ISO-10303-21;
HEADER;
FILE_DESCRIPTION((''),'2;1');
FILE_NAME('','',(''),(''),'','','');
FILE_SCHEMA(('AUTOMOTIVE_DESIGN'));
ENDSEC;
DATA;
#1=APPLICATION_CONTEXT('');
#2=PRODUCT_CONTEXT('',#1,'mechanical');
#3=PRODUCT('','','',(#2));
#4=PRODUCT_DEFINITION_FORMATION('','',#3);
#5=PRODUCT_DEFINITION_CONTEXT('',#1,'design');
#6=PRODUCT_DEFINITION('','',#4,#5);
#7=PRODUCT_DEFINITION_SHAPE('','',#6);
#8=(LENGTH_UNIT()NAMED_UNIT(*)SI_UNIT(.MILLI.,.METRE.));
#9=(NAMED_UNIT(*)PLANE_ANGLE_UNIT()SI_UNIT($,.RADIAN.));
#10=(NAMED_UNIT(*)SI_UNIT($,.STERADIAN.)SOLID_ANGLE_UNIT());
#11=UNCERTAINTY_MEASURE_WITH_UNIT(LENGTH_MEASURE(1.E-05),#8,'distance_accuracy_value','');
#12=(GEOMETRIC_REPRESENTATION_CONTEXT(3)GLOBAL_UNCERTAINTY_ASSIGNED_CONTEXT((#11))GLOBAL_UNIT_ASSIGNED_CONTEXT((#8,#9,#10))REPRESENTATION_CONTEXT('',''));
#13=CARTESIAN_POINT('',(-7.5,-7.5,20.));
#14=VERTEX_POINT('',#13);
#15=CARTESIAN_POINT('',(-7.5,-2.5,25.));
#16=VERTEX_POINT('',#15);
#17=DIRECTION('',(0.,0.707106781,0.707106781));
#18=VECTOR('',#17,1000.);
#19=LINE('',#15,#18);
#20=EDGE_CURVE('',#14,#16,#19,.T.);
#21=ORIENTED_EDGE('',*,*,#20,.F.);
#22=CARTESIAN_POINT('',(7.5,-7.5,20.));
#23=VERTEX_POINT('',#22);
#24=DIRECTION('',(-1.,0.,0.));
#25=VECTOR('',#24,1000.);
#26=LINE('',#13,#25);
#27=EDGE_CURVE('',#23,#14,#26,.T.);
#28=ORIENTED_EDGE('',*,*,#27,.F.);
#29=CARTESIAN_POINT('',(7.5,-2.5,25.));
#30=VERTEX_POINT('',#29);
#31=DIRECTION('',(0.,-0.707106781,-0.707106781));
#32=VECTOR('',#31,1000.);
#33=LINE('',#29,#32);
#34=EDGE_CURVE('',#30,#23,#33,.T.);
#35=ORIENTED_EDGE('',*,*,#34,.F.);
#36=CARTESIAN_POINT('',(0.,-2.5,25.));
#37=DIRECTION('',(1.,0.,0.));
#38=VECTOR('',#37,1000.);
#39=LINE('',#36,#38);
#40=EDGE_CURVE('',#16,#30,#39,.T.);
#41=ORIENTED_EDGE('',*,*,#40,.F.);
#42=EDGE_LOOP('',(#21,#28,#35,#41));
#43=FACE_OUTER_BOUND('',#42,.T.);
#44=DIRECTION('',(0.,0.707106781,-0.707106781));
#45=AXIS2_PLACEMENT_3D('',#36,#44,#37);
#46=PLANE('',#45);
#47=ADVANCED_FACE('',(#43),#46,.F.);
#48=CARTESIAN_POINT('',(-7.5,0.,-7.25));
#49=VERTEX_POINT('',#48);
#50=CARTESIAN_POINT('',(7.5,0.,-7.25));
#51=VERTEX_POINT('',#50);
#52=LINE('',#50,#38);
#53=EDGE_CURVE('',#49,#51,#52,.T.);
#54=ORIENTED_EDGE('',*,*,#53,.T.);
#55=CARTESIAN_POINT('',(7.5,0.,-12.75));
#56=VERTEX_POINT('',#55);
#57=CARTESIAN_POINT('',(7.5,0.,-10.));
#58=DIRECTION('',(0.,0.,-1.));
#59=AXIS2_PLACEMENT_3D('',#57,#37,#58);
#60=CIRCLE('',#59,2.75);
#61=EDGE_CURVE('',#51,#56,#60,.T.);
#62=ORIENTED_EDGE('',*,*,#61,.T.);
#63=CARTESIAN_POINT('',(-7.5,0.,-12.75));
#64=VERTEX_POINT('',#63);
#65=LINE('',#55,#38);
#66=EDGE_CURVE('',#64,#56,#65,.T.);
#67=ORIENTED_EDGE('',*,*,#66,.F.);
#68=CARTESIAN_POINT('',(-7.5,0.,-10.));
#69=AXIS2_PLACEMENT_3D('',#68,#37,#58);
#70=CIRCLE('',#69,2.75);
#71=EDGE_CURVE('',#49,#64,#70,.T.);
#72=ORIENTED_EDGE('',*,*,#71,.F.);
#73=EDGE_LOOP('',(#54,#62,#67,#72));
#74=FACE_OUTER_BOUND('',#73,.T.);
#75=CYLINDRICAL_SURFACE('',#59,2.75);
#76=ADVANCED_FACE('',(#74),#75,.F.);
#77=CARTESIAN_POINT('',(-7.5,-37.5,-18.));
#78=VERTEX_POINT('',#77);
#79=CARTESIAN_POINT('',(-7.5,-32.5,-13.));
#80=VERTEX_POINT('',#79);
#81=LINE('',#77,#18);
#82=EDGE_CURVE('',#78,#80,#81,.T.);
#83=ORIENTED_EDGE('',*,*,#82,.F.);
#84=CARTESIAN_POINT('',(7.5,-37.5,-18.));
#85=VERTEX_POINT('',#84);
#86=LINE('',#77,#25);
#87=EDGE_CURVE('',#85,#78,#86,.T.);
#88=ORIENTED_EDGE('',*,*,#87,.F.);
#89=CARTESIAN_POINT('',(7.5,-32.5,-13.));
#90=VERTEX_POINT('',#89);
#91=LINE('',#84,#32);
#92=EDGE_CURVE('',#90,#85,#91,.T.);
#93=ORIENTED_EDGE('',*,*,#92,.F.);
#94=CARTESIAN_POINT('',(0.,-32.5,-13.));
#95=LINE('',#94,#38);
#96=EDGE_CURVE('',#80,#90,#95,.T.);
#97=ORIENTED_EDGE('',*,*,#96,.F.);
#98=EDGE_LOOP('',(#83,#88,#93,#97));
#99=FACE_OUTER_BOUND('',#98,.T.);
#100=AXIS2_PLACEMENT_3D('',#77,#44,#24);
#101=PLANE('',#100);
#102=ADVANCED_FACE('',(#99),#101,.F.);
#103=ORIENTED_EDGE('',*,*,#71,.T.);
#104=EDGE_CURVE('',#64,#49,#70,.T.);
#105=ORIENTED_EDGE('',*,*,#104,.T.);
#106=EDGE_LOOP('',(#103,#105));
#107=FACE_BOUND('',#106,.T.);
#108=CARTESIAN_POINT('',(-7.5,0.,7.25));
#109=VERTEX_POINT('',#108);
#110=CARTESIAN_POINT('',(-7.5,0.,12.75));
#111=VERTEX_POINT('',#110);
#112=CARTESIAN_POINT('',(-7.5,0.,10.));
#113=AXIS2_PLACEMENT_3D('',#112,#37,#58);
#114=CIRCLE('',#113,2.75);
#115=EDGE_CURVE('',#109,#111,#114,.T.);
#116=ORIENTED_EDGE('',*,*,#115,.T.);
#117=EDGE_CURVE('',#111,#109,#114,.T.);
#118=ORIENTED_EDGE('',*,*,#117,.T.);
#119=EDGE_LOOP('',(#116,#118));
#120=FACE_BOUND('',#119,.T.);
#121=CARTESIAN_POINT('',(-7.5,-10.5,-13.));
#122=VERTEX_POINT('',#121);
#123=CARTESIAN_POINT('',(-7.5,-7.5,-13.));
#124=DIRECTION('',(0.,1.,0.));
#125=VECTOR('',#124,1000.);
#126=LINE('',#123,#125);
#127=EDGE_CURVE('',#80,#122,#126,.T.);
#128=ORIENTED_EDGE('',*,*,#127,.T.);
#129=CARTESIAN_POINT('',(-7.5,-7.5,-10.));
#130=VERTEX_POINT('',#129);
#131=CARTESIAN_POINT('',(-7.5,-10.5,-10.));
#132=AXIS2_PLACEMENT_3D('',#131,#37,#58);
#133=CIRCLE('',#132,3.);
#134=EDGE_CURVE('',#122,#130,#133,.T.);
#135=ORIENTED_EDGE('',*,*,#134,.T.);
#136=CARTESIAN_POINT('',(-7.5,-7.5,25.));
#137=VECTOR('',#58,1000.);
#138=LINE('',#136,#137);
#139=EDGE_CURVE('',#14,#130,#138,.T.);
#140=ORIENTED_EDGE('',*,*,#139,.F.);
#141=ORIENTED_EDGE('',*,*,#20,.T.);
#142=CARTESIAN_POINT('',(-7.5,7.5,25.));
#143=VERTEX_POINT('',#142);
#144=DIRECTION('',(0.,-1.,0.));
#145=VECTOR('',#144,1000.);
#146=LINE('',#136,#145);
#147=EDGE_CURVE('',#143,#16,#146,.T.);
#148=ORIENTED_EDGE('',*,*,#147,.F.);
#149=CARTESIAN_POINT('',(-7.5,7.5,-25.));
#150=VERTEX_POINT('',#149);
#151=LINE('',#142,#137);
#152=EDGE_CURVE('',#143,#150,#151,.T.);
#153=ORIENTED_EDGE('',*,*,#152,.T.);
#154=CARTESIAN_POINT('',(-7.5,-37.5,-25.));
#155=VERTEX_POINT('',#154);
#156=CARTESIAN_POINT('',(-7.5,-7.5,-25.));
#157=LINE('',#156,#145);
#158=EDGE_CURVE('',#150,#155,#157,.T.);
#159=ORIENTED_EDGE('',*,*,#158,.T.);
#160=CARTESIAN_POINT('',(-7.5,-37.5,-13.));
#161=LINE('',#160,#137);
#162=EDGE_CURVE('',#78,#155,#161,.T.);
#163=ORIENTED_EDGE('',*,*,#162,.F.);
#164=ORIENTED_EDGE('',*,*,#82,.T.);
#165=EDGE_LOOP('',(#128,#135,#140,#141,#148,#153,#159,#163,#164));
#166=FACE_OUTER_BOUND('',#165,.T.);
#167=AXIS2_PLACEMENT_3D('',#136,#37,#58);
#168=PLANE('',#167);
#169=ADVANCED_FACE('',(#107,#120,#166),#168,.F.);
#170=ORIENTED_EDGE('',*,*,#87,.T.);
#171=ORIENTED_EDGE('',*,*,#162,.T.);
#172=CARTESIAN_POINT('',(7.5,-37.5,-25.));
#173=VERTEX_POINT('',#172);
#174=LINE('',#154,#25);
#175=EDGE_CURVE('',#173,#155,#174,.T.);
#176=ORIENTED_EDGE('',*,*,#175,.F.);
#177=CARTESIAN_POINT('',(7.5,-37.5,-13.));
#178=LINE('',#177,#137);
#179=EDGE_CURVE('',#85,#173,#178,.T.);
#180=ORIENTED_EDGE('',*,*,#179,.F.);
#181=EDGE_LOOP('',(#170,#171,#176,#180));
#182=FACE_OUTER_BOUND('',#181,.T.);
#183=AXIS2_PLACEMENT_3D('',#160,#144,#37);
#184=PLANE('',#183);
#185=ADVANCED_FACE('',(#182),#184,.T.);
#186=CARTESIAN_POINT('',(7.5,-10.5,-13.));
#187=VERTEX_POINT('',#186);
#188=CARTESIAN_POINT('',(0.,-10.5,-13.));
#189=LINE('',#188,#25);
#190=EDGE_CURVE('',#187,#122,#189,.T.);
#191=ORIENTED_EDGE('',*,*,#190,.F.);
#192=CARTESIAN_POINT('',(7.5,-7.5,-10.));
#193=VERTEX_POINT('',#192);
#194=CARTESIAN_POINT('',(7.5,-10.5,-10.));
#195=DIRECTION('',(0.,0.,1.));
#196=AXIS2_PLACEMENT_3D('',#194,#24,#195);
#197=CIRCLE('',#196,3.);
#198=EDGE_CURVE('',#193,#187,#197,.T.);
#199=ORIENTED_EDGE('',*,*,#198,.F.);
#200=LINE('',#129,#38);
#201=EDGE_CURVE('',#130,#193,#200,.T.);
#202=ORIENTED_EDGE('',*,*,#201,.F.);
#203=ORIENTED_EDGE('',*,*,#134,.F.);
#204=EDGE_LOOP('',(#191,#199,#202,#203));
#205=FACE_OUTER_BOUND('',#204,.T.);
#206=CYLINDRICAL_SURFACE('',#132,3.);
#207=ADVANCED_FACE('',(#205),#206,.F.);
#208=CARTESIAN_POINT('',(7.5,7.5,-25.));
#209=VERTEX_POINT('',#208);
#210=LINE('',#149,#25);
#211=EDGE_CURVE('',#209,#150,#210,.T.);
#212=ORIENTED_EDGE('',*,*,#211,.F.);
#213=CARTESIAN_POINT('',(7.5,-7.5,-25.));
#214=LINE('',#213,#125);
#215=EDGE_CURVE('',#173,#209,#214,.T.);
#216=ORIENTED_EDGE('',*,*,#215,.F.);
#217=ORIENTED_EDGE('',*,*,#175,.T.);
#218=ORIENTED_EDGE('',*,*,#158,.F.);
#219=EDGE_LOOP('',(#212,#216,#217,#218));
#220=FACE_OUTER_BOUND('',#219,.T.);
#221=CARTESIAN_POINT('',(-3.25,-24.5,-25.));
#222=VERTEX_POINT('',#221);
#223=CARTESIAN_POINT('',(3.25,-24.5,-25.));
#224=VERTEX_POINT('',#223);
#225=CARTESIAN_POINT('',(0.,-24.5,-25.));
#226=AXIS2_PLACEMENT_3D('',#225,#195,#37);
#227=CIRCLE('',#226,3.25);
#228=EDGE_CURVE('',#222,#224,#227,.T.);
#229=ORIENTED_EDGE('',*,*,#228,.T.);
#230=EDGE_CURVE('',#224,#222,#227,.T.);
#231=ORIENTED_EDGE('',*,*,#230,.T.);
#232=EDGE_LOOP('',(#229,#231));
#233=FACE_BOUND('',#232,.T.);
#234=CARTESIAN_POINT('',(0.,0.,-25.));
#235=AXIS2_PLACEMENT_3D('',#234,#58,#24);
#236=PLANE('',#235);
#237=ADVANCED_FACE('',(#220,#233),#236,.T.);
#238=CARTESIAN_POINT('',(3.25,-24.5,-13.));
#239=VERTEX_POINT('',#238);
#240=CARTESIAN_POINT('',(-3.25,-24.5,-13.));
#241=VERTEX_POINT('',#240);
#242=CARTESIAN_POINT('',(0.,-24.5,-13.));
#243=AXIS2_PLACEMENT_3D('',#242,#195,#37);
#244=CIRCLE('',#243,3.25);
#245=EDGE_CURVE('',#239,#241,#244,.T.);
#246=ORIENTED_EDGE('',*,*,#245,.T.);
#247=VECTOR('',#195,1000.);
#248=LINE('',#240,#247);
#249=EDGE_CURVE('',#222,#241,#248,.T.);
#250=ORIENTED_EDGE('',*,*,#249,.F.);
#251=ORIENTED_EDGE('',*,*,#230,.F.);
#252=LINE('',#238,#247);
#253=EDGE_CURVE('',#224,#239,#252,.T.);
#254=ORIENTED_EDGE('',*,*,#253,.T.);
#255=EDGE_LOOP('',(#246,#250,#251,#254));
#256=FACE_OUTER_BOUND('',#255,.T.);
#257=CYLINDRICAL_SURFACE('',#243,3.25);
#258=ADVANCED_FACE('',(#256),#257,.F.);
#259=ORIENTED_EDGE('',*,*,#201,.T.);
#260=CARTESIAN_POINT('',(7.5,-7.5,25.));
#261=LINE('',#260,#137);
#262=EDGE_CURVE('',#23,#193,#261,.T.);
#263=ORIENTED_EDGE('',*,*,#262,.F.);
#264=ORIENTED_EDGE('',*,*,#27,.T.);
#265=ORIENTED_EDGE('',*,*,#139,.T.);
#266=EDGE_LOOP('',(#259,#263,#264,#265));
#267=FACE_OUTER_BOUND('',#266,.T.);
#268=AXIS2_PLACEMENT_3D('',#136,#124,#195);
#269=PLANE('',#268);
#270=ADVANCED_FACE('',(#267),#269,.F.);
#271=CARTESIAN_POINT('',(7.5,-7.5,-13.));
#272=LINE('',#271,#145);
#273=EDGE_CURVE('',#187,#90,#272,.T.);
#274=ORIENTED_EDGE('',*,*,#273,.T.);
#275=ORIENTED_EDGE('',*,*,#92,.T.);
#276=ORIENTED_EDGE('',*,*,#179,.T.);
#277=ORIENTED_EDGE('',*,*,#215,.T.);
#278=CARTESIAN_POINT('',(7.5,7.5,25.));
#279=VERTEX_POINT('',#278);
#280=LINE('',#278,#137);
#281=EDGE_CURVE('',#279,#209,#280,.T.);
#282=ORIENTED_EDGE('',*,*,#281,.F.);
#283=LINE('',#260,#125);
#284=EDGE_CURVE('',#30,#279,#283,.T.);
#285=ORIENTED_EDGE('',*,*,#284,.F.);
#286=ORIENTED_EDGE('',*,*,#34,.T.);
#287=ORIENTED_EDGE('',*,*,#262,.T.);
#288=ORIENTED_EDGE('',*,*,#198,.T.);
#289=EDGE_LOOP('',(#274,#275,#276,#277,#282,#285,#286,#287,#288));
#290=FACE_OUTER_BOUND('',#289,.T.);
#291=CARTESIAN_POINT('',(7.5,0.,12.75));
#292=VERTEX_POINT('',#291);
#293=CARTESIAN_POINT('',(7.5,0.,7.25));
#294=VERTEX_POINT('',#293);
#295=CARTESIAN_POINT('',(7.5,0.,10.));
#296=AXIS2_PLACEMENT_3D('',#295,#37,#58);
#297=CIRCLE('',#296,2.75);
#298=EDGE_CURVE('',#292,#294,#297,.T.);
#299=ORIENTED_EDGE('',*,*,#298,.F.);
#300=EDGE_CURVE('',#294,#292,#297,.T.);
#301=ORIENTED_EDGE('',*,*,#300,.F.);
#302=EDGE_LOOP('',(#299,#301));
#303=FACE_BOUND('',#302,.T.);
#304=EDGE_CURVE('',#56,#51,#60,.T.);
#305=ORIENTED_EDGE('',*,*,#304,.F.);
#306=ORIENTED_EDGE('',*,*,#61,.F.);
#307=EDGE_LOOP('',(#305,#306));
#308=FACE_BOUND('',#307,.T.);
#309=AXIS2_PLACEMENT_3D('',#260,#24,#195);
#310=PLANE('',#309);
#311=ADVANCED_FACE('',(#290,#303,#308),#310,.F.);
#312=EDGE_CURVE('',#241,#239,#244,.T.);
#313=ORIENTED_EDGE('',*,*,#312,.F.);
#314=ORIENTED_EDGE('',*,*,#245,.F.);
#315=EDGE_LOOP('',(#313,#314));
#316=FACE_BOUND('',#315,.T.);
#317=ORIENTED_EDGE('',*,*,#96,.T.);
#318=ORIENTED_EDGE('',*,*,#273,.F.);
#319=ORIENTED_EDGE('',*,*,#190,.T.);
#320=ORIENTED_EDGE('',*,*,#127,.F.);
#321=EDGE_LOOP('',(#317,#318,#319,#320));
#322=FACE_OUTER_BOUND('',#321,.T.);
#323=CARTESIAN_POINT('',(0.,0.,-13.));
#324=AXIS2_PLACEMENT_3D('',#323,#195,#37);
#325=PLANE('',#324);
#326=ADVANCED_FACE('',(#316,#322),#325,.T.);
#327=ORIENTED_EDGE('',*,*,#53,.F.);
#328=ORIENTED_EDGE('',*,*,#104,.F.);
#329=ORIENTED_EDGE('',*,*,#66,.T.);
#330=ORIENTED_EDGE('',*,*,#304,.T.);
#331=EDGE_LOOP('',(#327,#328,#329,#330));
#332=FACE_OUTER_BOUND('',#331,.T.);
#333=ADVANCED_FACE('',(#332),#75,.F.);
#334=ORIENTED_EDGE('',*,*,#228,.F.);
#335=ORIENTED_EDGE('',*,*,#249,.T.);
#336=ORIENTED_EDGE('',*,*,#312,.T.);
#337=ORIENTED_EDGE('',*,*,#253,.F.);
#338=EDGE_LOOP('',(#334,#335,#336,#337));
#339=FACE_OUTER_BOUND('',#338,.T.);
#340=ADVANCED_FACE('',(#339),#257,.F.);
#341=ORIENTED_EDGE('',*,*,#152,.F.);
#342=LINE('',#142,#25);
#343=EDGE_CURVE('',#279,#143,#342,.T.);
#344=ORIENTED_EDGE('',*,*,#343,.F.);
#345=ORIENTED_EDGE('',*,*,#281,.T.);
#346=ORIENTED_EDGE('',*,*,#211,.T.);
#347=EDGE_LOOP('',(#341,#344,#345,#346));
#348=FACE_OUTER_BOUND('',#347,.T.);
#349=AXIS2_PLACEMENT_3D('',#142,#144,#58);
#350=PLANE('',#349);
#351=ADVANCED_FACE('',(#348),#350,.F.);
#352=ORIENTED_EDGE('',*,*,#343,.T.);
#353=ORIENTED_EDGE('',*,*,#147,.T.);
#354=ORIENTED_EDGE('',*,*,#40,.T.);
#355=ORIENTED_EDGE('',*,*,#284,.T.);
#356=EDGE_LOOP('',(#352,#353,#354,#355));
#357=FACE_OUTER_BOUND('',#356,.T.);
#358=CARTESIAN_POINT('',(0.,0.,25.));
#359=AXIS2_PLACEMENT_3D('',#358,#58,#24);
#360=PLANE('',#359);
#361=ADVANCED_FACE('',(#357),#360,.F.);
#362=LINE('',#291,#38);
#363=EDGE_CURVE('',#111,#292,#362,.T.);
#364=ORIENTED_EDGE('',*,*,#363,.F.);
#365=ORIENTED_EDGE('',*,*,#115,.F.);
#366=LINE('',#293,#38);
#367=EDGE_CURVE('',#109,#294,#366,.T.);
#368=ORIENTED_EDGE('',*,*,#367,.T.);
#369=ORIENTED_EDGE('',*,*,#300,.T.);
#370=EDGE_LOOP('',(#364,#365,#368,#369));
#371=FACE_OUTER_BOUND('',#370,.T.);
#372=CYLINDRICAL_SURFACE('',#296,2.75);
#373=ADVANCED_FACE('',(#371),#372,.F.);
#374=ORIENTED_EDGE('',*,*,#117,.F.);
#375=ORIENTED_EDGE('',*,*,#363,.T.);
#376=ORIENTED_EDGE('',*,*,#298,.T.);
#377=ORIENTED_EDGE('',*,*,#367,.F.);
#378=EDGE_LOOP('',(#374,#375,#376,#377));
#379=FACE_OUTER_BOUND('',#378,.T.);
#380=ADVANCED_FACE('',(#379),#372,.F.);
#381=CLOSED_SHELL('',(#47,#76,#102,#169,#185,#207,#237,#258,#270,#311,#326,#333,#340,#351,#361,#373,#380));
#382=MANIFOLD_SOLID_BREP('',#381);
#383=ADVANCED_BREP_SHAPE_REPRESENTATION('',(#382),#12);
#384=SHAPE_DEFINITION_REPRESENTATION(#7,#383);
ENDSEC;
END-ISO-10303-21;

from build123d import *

# Parameters (mm, degrees)
SKETCH_1_W              = 15
SKETCH_1_H              = 15
EXTRUDE_1_DEPTH         = 25
SKETCH_2_W              = 15
SKETCH_2_H              = 30
EXTRUDE_2_DEPTH         = 12
HOLE_WIZARD_6_5_6_5_1_D = 6.5
FILLET_1_R              = 3
CHAMFER_2_SIZE          = 5
HOLE_WIZARD_5_5_5_5_1_D = 5.5


with BuildPart() as part:
    # 草图1 → 凸台-拉伸1 (new, symmetric)
    with BuildSketch(Plane.XY):
        Rectangle(SKETCH_1_W, SKETCH_1_H)
    extrude(amount=EXTRUDE_1_DEPTH, both=True)

    # 草图2 → 凸台-拉伸2 (add)
    with BuildSketch(Plane(origin=(0, 0, -25), x_dir=(-1, 0, 0), z_dir=(0, 0, -1))):
        with Locations((0, -22.5)):
            Rectangle(SKETCH_2_W, SKETCH_2_H)
    extrude(amount=-EXTRUDE_2_DEPTH)

    # Ø6.5 (6.5) 直径孔1 (through all)
    with Locations(Plane.XY.offset(-13)):
        with Locations((0, -24.5)):
            Hole(HOLE_WIZARD_6_5_6_5_1_D / 2)

    # 圆角1
    fillet_1_edges = [part.edges().sort_by_distance(p)[0] for p in [
        (0, -7.5, -13),
    ]]
    fillet(fillet_1_edges, radius=FILLET_1_R)

    # 倒角2
    chamfer_2_edges = [part.edges().sort_by_distance(p)[0] for p in [
        (0, -37.5, -13),
        (0, -7.5, 25),
    ]]
    chamfer(chamfer_2_edges, length=CHAMFER_2_SIZE)

    # Ø5.5 (5.5) 直径孔1 (through all)
    with Locations(Plane(origin=(7.5, 0, 0), x_dir=(0, 0, -1), z_dir=(1, 0, 0))):
        with Locations((10, 0), (-10, 0)):
            Hole(HOLE_WIZARD_5_5_5_5_1_D / 2)


solid = part.part
